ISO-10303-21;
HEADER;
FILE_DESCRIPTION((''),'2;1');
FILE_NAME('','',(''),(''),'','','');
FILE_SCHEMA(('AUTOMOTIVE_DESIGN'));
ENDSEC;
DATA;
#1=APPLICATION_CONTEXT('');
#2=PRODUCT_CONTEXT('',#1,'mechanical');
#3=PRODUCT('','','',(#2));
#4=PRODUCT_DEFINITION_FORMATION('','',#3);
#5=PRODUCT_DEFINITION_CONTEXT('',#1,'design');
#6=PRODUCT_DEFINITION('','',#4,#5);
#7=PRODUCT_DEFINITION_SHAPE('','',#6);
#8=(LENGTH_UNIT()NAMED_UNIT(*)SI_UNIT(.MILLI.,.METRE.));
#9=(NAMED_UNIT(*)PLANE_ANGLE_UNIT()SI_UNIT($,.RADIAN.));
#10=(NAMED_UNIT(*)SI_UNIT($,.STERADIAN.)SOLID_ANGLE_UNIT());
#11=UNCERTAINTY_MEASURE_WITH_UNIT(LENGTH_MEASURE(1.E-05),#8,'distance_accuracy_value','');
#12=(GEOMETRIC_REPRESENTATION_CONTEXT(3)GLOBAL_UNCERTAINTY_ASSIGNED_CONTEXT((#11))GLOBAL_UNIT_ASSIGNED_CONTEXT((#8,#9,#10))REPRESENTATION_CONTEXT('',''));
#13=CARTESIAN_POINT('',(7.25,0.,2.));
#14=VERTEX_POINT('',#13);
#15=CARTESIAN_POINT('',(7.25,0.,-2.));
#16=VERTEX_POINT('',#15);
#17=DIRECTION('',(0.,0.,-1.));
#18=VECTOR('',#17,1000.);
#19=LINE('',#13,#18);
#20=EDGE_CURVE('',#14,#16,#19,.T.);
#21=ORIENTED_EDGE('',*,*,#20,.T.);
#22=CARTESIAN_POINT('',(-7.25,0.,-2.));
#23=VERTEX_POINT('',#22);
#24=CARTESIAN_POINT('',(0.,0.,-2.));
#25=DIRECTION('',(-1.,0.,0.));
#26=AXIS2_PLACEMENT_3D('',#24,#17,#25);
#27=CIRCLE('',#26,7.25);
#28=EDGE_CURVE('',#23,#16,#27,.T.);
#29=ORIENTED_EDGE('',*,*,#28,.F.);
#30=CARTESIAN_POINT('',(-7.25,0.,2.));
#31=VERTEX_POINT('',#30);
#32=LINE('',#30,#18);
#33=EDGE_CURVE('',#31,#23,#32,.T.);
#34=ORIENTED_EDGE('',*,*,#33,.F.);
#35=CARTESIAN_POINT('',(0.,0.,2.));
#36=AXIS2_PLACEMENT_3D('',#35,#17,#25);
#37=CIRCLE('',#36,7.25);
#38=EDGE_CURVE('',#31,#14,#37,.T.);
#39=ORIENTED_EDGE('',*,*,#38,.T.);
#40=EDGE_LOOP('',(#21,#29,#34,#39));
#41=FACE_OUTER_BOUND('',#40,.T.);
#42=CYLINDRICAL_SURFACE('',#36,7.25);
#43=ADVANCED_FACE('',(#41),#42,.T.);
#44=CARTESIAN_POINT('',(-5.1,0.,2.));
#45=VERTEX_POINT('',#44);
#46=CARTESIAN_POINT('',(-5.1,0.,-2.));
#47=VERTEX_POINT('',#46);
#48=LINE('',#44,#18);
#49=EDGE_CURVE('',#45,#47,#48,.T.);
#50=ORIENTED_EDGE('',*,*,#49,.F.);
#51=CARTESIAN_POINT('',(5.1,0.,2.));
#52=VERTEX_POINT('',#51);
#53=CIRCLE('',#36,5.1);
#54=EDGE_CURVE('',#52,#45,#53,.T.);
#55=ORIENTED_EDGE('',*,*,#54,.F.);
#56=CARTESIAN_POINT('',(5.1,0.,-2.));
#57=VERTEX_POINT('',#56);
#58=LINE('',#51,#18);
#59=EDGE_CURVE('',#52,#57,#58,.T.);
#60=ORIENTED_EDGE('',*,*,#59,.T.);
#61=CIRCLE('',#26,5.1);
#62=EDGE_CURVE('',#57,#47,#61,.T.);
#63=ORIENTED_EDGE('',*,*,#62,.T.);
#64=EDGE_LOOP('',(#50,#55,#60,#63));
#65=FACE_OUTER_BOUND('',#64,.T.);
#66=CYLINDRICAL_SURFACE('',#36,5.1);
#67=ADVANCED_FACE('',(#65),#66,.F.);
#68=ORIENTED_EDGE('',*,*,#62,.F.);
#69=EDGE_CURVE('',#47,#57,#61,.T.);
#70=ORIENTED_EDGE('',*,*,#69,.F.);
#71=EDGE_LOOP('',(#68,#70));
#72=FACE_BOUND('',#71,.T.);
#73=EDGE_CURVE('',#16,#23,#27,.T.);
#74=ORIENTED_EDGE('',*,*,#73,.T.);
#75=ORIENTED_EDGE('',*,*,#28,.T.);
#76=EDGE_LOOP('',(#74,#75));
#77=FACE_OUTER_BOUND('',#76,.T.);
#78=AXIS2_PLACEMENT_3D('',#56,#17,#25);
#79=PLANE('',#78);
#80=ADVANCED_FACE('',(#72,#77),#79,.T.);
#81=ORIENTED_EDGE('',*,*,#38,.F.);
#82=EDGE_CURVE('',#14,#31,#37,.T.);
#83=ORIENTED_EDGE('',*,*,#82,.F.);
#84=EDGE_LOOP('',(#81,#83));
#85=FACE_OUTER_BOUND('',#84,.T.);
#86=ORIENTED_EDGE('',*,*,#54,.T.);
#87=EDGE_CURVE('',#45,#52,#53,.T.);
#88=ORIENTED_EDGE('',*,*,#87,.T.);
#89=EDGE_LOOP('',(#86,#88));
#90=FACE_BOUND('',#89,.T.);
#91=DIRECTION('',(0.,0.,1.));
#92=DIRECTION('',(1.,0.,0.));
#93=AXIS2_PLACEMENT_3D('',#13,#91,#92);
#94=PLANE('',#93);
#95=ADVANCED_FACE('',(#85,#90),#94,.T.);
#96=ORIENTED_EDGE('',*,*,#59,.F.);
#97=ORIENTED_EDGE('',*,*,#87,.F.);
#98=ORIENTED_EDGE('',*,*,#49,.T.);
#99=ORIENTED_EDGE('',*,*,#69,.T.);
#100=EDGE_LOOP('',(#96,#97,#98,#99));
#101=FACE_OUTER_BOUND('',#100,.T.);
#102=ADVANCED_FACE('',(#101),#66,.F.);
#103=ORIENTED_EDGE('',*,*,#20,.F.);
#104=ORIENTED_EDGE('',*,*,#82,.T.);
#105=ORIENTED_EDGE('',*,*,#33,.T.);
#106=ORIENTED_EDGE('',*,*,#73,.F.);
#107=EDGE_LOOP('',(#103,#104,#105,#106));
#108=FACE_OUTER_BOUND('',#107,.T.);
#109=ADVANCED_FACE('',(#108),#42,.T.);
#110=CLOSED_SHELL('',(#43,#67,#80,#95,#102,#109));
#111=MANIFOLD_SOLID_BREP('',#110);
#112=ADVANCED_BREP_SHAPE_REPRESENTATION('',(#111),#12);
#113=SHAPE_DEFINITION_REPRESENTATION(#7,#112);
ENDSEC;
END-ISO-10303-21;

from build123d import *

# Parameters (mm, degrees)
SKETCH1_W = 2.15
SKETCH1_H = 4


with BuildPart() as part:
    # Sketch1 → Revolve1 (revolve)
    with BuildSketch(Plane.XZ, mode=Mode.PRIVATE) as revolve1_sk:
        with Locations((6.175, 0)):
            Rectangle(SKETCH1_W, SKETCH1_H)
    revolve(revolve1_sk.sketch.rotate(Axis((0, 0, 2), (0, 0, -1)), 180), axis=Axis((0, 0, 2), (0, 0, -1)))


solid = part.part
